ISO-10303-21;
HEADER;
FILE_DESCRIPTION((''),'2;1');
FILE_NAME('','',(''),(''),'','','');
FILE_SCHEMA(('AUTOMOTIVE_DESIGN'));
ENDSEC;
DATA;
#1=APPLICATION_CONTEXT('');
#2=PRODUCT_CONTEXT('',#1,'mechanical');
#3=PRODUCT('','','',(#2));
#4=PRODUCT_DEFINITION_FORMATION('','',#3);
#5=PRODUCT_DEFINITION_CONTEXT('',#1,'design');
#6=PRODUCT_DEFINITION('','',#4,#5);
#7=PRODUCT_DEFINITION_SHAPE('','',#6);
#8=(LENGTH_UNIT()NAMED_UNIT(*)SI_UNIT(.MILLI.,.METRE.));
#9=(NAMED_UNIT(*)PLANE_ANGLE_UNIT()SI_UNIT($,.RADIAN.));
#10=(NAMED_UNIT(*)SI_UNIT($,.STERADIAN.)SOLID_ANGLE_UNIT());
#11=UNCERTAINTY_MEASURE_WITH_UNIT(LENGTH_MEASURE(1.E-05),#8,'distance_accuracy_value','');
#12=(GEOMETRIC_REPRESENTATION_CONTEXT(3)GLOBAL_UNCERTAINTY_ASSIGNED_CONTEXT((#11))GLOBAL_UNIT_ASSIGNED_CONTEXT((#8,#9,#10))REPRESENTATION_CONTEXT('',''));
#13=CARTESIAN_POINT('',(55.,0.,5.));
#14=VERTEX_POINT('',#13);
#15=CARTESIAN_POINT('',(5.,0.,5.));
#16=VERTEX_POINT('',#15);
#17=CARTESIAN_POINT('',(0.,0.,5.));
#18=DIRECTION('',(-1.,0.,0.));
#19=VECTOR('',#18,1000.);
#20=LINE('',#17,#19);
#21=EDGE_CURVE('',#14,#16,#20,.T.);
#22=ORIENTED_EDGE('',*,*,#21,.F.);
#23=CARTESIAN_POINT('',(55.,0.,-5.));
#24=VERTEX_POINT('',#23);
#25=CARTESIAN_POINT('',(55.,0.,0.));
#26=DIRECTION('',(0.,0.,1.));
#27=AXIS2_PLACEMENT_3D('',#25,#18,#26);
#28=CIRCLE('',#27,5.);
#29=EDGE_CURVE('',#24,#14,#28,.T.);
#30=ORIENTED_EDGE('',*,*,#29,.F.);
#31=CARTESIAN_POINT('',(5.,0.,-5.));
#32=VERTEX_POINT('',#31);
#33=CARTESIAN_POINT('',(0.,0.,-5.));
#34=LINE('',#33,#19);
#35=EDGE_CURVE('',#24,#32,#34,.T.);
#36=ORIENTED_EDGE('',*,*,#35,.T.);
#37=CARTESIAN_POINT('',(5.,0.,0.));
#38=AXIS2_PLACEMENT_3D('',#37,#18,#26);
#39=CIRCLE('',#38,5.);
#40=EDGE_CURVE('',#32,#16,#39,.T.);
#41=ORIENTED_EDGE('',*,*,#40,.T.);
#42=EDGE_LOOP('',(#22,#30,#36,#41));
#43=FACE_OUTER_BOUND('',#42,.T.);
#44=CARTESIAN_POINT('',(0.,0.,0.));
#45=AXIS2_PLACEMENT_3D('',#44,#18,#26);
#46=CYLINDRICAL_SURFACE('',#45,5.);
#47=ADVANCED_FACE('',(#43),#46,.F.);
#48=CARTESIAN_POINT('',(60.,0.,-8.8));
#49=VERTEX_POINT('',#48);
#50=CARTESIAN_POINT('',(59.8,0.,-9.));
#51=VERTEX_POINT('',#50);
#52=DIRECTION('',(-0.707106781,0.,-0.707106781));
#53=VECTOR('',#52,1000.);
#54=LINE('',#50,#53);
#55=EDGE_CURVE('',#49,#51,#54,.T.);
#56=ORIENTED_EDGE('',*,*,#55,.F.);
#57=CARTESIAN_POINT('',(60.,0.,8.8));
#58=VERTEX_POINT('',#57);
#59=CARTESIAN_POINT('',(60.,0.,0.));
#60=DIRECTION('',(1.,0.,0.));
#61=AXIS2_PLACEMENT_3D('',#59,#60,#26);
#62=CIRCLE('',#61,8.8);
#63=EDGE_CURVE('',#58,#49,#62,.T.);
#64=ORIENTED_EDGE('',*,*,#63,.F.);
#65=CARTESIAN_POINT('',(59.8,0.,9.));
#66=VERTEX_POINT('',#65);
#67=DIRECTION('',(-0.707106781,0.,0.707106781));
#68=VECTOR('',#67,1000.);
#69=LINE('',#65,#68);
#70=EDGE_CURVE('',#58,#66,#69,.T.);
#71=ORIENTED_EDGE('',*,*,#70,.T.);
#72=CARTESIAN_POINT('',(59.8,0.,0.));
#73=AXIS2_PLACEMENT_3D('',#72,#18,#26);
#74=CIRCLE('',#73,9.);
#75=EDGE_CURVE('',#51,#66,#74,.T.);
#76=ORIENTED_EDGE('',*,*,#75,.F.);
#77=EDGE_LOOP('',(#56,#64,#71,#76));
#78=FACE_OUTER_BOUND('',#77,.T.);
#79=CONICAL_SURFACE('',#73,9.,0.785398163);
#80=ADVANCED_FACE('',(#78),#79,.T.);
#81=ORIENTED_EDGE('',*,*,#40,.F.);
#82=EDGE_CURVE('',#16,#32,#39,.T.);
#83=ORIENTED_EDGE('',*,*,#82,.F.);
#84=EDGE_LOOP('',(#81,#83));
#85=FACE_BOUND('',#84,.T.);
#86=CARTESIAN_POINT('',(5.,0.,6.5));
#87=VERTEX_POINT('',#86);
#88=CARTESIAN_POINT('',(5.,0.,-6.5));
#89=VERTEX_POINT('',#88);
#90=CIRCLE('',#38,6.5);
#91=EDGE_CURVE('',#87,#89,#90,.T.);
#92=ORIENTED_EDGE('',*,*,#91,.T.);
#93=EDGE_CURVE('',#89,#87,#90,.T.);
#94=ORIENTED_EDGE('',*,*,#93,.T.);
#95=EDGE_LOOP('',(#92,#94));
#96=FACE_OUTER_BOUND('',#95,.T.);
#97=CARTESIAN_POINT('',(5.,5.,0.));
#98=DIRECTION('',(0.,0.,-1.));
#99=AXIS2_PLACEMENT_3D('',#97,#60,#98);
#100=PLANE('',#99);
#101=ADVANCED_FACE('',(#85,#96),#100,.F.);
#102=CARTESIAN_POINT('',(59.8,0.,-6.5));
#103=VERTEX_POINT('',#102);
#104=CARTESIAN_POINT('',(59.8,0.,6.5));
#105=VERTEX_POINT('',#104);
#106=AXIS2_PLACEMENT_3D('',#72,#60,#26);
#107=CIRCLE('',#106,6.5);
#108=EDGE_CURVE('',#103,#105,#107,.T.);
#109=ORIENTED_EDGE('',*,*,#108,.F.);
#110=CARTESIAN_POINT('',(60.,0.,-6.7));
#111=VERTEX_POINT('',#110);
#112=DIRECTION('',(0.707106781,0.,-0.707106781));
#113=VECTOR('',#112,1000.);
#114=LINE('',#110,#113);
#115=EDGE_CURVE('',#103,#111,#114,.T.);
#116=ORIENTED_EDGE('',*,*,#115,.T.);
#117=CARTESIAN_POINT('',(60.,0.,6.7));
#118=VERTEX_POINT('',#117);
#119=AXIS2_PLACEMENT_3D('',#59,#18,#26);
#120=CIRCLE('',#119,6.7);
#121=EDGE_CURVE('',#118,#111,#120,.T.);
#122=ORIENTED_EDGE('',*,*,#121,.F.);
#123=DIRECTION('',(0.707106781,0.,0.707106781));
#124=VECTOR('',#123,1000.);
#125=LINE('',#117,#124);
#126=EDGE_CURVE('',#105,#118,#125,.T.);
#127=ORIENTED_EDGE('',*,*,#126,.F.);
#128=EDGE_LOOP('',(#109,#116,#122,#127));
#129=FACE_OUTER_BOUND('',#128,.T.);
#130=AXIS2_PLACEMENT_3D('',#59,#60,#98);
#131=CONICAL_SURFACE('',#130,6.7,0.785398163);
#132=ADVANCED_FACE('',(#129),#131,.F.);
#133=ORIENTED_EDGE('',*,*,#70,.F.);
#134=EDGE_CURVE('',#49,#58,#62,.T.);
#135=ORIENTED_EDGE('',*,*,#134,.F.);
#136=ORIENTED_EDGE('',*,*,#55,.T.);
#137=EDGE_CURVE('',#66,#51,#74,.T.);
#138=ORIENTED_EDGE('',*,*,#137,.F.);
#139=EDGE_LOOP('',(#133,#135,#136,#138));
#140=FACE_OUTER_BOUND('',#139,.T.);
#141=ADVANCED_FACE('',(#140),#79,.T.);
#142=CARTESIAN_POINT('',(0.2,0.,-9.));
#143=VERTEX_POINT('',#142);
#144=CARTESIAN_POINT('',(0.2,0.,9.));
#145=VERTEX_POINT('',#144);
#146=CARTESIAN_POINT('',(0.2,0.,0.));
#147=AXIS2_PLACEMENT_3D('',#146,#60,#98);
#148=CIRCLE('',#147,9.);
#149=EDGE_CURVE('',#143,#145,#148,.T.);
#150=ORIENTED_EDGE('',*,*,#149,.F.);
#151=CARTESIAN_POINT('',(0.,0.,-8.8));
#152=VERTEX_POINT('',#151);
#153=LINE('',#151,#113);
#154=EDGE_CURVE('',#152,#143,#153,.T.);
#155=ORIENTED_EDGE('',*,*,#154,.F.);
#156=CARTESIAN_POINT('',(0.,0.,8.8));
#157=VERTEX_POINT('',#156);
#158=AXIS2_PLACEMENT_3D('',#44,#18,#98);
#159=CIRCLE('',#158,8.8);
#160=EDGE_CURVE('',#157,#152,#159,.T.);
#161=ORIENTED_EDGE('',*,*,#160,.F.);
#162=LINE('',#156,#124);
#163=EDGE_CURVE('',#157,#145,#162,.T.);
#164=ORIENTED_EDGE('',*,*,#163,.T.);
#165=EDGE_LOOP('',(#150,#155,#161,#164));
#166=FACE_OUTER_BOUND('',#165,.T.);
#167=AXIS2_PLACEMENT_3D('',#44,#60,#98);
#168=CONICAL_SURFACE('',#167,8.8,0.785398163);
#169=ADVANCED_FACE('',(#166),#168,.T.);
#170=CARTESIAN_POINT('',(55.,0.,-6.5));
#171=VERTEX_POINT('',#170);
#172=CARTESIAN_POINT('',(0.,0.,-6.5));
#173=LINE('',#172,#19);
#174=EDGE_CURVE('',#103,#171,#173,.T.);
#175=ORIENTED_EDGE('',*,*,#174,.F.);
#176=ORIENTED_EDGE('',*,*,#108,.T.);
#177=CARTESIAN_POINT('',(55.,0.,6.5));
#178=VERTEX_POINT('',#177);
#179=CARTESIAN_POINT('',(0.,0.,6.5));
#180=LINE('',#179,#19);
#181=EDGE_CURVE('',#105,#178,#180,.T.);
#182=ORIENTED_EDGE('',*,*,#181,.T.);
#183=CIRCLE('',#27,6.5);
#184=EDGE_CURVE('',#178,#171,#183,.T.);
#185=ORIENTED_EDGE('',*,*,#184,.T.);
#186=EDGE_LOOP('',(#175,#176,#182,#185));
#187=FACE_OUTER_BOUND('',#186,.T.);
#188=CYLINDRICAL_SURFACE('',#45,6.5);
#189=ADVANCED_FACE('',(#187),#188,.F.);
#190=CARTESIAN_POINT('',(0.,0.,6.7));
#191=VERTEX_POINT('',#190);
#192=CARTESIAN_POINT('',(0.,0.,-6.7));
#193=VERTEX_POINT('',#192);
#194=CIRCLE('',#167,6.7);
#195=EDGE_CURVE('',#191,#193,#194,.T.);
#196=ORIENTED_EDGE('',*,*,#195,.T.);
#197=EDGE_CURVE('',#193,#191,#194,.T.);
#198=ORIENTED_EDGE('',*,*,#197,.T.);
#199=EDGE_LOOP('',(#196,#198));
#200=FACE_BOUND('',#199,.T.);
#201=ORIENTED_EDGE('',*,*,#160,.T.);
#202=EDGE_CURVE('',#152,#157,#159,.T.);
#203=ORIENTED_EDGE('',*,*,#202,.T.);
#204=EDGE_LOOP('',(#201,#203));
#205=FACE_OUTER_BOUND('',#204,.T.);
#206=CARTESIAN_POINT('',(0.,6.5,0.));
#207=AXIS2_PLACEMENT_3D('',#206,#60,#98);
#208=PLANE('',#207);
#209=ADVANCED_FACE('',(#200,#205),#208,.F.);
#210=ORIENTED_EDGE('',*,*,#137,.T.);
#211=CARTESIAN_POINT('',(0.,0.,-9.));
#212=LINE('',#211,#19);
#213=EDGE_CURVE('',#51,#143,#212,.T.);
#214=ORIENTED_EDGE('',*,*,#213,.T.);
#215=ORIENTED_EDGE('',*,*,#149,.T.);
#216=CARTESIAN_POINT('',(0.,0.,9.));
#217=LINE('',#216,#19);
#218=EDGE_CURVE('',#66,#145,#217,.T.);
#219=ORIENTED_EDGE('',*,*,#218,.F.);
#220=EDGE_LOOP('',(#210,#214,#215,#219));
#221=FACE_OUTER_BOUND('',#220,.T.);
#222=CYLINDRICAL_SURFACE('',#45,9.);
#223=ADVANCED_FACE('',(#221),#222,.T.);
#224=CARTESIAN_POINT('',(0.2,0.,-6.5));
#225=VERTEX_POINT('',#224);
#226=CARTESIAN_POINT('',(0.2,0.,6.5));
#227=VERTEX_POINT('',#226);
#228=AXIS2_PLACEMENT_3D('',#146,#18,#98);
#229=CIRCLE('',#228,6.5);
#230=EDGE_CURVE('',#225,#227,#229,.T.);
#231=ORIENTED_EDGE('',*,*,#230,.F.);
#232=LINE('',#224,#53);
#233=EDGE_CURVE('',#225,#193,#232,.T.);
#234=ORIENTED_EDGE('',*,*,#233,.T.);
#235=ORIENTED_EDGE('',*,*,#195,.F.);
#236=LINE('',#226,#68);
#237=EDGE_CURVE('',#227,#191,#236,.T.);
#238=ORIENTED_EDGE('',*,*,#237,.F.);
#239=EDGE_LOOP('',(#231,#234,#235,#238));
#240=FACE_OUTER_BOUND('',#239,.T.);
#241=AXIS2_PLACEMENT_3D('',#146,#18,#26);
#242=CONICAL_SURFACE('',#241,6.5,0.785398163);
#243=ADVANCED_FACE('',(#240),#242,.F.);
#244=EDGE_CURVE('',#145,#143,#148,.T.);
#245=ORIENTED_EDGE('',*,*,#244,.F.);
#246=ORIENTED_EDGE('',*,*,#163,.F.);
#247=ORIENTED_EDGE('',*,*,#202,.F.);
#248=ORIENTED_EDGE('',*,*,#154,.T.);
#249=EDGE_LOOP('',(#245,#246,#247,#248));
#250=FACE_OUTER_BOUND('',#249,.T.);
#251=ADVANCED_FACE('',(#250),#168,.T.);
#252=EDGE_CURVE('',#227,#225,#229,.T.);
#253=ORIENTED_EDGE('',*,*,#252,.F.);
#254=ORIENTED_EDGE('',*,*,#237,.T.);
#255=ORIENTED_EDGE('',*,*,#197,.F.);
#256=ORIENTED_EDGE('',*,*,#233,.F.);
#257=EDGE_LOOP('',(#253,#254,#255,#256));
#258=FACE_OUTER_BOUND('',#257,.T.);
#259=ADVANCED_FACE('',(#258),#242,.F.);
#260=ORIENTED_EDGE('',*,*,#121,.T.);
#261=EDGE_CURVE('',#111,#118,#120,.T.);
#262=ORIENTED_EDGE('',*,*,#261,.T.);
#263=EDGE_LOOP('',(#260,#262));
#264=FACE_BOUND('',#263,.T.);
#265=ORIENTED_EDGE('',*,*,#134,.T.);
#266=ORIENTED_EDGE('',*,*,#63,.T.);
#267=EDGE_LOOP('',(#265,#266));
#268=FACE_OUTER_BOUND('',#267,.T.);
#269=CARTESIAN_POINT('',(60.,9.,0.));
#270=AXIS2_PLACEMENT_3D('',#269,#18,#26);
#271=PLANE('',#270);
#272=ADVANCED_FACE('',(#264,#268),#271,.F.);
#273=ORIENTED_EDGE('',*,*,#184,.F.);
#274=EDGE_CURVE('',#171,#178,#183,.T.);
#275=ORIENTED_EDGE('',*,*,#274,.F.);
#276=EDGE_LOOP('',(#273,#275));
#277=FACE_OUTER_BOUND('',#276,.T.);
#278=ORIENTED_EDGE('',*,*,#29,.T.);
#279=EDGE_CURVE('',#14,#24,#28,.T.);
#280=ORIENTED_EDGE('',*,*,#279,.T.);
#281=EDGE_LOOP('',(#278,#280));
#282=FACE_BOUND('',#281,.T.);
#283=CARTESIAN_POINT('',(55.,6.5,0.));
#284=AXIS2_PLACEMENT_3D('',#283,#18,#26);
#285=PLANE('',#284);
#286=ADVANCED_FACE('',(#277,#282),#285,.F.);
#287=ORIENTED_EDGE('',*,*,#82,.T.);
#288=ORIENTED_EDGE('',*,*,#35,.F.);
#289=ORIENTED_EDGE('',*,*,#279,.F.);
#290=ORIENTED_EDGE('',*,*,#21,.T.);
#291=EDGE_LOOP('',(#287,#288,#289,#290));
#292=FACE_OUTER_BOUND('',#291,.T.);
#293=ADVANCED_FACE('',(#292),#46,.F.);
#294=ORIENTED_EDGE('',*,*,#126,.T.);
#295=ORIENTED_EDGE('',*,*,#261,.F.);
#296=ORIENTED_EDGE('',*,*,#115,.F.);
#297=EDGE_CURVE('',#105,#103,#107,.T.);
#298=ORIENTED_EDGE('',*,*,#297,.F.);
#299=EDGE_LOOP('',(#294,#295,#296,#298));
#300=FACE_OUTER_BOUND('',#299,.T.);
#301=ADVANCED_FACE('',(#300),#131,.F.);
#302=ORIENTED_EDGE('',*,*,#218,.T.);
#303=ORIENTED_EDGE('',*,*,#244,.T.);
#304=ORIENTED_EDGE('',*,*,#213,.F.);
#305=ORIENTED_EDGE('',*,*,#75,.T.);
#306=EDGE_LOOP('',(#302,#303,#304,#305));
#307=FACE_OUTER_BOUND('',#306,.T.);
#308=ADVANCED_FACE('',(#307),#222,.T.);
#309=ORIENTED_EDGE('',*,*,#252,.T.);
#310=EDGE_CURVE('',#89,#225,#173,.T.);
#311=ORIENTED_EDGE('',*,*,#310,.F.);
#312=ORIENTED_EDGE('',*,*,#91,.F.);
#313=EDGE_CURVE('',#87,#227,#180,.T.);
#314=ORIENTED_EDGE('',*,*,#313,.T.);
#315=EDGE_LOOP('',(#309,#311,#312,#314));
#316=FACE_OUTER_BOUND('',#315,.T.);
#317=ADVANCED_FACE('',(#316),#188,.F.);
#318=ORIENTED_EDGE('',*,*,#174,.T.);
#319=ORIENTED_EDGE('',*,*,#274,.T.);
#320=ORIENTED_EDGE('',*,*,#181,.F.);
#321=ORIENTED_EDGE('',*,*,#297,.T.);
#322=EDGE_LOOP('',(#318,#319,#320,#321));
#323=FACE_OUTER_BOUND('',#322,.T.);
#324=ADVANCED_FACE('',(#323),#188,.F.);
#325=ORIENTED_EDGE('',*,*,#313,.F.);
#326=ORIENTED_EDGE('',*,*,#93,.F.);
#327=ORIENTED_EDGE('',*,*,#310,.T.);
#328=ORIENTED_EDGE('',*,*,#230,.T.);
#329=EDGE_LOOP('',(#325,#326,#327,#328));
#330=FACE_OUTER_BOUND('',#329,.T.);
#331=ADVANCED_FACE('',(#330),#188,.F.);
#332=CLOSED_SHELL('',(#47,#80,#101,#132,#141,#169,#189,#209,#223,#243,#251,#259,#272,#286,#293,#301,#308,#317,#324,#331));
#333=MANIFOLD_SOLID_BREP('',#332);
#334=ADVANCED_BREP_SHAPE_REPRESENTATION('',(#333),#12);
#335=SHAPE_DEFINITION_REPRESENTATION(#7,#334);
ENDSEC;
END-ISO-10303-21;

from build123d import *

# Parameters (mm, degrees)
CHAMFER1_SIZE = 0.2


with BuildPart() as part:
    # Sketch1 → Revolve1 (revolve)
    with BuildSketch(Plane.XY, mode=Mode.PRIVATE) as revolve1_sk:
        Polygon((0, 9), (60, 9), (60, 6.5), (55, 6.5), (55, 5), (5, 5), (5, 6.5), (0, 6.5), align=None)
    revolve(revolve1_sk.sketch.rotate(Axis((0, 0, 0), (1, 0, 0)), 90), axis=Axis((0, 0, 0), (1, 0, 0)))

    # Chamfer1
    chamfer1_edges = [part.edges().sort_by_distance(p)[0] for p in [
        (0, 0, -6.5),
        (60, 0, -6.5),
        (60, 0, -9),
        (0, 0, -9),
    ]]
    chamfer(chamfer1_edges, length=CHAMFER1_SIZE)


solid = part.part
